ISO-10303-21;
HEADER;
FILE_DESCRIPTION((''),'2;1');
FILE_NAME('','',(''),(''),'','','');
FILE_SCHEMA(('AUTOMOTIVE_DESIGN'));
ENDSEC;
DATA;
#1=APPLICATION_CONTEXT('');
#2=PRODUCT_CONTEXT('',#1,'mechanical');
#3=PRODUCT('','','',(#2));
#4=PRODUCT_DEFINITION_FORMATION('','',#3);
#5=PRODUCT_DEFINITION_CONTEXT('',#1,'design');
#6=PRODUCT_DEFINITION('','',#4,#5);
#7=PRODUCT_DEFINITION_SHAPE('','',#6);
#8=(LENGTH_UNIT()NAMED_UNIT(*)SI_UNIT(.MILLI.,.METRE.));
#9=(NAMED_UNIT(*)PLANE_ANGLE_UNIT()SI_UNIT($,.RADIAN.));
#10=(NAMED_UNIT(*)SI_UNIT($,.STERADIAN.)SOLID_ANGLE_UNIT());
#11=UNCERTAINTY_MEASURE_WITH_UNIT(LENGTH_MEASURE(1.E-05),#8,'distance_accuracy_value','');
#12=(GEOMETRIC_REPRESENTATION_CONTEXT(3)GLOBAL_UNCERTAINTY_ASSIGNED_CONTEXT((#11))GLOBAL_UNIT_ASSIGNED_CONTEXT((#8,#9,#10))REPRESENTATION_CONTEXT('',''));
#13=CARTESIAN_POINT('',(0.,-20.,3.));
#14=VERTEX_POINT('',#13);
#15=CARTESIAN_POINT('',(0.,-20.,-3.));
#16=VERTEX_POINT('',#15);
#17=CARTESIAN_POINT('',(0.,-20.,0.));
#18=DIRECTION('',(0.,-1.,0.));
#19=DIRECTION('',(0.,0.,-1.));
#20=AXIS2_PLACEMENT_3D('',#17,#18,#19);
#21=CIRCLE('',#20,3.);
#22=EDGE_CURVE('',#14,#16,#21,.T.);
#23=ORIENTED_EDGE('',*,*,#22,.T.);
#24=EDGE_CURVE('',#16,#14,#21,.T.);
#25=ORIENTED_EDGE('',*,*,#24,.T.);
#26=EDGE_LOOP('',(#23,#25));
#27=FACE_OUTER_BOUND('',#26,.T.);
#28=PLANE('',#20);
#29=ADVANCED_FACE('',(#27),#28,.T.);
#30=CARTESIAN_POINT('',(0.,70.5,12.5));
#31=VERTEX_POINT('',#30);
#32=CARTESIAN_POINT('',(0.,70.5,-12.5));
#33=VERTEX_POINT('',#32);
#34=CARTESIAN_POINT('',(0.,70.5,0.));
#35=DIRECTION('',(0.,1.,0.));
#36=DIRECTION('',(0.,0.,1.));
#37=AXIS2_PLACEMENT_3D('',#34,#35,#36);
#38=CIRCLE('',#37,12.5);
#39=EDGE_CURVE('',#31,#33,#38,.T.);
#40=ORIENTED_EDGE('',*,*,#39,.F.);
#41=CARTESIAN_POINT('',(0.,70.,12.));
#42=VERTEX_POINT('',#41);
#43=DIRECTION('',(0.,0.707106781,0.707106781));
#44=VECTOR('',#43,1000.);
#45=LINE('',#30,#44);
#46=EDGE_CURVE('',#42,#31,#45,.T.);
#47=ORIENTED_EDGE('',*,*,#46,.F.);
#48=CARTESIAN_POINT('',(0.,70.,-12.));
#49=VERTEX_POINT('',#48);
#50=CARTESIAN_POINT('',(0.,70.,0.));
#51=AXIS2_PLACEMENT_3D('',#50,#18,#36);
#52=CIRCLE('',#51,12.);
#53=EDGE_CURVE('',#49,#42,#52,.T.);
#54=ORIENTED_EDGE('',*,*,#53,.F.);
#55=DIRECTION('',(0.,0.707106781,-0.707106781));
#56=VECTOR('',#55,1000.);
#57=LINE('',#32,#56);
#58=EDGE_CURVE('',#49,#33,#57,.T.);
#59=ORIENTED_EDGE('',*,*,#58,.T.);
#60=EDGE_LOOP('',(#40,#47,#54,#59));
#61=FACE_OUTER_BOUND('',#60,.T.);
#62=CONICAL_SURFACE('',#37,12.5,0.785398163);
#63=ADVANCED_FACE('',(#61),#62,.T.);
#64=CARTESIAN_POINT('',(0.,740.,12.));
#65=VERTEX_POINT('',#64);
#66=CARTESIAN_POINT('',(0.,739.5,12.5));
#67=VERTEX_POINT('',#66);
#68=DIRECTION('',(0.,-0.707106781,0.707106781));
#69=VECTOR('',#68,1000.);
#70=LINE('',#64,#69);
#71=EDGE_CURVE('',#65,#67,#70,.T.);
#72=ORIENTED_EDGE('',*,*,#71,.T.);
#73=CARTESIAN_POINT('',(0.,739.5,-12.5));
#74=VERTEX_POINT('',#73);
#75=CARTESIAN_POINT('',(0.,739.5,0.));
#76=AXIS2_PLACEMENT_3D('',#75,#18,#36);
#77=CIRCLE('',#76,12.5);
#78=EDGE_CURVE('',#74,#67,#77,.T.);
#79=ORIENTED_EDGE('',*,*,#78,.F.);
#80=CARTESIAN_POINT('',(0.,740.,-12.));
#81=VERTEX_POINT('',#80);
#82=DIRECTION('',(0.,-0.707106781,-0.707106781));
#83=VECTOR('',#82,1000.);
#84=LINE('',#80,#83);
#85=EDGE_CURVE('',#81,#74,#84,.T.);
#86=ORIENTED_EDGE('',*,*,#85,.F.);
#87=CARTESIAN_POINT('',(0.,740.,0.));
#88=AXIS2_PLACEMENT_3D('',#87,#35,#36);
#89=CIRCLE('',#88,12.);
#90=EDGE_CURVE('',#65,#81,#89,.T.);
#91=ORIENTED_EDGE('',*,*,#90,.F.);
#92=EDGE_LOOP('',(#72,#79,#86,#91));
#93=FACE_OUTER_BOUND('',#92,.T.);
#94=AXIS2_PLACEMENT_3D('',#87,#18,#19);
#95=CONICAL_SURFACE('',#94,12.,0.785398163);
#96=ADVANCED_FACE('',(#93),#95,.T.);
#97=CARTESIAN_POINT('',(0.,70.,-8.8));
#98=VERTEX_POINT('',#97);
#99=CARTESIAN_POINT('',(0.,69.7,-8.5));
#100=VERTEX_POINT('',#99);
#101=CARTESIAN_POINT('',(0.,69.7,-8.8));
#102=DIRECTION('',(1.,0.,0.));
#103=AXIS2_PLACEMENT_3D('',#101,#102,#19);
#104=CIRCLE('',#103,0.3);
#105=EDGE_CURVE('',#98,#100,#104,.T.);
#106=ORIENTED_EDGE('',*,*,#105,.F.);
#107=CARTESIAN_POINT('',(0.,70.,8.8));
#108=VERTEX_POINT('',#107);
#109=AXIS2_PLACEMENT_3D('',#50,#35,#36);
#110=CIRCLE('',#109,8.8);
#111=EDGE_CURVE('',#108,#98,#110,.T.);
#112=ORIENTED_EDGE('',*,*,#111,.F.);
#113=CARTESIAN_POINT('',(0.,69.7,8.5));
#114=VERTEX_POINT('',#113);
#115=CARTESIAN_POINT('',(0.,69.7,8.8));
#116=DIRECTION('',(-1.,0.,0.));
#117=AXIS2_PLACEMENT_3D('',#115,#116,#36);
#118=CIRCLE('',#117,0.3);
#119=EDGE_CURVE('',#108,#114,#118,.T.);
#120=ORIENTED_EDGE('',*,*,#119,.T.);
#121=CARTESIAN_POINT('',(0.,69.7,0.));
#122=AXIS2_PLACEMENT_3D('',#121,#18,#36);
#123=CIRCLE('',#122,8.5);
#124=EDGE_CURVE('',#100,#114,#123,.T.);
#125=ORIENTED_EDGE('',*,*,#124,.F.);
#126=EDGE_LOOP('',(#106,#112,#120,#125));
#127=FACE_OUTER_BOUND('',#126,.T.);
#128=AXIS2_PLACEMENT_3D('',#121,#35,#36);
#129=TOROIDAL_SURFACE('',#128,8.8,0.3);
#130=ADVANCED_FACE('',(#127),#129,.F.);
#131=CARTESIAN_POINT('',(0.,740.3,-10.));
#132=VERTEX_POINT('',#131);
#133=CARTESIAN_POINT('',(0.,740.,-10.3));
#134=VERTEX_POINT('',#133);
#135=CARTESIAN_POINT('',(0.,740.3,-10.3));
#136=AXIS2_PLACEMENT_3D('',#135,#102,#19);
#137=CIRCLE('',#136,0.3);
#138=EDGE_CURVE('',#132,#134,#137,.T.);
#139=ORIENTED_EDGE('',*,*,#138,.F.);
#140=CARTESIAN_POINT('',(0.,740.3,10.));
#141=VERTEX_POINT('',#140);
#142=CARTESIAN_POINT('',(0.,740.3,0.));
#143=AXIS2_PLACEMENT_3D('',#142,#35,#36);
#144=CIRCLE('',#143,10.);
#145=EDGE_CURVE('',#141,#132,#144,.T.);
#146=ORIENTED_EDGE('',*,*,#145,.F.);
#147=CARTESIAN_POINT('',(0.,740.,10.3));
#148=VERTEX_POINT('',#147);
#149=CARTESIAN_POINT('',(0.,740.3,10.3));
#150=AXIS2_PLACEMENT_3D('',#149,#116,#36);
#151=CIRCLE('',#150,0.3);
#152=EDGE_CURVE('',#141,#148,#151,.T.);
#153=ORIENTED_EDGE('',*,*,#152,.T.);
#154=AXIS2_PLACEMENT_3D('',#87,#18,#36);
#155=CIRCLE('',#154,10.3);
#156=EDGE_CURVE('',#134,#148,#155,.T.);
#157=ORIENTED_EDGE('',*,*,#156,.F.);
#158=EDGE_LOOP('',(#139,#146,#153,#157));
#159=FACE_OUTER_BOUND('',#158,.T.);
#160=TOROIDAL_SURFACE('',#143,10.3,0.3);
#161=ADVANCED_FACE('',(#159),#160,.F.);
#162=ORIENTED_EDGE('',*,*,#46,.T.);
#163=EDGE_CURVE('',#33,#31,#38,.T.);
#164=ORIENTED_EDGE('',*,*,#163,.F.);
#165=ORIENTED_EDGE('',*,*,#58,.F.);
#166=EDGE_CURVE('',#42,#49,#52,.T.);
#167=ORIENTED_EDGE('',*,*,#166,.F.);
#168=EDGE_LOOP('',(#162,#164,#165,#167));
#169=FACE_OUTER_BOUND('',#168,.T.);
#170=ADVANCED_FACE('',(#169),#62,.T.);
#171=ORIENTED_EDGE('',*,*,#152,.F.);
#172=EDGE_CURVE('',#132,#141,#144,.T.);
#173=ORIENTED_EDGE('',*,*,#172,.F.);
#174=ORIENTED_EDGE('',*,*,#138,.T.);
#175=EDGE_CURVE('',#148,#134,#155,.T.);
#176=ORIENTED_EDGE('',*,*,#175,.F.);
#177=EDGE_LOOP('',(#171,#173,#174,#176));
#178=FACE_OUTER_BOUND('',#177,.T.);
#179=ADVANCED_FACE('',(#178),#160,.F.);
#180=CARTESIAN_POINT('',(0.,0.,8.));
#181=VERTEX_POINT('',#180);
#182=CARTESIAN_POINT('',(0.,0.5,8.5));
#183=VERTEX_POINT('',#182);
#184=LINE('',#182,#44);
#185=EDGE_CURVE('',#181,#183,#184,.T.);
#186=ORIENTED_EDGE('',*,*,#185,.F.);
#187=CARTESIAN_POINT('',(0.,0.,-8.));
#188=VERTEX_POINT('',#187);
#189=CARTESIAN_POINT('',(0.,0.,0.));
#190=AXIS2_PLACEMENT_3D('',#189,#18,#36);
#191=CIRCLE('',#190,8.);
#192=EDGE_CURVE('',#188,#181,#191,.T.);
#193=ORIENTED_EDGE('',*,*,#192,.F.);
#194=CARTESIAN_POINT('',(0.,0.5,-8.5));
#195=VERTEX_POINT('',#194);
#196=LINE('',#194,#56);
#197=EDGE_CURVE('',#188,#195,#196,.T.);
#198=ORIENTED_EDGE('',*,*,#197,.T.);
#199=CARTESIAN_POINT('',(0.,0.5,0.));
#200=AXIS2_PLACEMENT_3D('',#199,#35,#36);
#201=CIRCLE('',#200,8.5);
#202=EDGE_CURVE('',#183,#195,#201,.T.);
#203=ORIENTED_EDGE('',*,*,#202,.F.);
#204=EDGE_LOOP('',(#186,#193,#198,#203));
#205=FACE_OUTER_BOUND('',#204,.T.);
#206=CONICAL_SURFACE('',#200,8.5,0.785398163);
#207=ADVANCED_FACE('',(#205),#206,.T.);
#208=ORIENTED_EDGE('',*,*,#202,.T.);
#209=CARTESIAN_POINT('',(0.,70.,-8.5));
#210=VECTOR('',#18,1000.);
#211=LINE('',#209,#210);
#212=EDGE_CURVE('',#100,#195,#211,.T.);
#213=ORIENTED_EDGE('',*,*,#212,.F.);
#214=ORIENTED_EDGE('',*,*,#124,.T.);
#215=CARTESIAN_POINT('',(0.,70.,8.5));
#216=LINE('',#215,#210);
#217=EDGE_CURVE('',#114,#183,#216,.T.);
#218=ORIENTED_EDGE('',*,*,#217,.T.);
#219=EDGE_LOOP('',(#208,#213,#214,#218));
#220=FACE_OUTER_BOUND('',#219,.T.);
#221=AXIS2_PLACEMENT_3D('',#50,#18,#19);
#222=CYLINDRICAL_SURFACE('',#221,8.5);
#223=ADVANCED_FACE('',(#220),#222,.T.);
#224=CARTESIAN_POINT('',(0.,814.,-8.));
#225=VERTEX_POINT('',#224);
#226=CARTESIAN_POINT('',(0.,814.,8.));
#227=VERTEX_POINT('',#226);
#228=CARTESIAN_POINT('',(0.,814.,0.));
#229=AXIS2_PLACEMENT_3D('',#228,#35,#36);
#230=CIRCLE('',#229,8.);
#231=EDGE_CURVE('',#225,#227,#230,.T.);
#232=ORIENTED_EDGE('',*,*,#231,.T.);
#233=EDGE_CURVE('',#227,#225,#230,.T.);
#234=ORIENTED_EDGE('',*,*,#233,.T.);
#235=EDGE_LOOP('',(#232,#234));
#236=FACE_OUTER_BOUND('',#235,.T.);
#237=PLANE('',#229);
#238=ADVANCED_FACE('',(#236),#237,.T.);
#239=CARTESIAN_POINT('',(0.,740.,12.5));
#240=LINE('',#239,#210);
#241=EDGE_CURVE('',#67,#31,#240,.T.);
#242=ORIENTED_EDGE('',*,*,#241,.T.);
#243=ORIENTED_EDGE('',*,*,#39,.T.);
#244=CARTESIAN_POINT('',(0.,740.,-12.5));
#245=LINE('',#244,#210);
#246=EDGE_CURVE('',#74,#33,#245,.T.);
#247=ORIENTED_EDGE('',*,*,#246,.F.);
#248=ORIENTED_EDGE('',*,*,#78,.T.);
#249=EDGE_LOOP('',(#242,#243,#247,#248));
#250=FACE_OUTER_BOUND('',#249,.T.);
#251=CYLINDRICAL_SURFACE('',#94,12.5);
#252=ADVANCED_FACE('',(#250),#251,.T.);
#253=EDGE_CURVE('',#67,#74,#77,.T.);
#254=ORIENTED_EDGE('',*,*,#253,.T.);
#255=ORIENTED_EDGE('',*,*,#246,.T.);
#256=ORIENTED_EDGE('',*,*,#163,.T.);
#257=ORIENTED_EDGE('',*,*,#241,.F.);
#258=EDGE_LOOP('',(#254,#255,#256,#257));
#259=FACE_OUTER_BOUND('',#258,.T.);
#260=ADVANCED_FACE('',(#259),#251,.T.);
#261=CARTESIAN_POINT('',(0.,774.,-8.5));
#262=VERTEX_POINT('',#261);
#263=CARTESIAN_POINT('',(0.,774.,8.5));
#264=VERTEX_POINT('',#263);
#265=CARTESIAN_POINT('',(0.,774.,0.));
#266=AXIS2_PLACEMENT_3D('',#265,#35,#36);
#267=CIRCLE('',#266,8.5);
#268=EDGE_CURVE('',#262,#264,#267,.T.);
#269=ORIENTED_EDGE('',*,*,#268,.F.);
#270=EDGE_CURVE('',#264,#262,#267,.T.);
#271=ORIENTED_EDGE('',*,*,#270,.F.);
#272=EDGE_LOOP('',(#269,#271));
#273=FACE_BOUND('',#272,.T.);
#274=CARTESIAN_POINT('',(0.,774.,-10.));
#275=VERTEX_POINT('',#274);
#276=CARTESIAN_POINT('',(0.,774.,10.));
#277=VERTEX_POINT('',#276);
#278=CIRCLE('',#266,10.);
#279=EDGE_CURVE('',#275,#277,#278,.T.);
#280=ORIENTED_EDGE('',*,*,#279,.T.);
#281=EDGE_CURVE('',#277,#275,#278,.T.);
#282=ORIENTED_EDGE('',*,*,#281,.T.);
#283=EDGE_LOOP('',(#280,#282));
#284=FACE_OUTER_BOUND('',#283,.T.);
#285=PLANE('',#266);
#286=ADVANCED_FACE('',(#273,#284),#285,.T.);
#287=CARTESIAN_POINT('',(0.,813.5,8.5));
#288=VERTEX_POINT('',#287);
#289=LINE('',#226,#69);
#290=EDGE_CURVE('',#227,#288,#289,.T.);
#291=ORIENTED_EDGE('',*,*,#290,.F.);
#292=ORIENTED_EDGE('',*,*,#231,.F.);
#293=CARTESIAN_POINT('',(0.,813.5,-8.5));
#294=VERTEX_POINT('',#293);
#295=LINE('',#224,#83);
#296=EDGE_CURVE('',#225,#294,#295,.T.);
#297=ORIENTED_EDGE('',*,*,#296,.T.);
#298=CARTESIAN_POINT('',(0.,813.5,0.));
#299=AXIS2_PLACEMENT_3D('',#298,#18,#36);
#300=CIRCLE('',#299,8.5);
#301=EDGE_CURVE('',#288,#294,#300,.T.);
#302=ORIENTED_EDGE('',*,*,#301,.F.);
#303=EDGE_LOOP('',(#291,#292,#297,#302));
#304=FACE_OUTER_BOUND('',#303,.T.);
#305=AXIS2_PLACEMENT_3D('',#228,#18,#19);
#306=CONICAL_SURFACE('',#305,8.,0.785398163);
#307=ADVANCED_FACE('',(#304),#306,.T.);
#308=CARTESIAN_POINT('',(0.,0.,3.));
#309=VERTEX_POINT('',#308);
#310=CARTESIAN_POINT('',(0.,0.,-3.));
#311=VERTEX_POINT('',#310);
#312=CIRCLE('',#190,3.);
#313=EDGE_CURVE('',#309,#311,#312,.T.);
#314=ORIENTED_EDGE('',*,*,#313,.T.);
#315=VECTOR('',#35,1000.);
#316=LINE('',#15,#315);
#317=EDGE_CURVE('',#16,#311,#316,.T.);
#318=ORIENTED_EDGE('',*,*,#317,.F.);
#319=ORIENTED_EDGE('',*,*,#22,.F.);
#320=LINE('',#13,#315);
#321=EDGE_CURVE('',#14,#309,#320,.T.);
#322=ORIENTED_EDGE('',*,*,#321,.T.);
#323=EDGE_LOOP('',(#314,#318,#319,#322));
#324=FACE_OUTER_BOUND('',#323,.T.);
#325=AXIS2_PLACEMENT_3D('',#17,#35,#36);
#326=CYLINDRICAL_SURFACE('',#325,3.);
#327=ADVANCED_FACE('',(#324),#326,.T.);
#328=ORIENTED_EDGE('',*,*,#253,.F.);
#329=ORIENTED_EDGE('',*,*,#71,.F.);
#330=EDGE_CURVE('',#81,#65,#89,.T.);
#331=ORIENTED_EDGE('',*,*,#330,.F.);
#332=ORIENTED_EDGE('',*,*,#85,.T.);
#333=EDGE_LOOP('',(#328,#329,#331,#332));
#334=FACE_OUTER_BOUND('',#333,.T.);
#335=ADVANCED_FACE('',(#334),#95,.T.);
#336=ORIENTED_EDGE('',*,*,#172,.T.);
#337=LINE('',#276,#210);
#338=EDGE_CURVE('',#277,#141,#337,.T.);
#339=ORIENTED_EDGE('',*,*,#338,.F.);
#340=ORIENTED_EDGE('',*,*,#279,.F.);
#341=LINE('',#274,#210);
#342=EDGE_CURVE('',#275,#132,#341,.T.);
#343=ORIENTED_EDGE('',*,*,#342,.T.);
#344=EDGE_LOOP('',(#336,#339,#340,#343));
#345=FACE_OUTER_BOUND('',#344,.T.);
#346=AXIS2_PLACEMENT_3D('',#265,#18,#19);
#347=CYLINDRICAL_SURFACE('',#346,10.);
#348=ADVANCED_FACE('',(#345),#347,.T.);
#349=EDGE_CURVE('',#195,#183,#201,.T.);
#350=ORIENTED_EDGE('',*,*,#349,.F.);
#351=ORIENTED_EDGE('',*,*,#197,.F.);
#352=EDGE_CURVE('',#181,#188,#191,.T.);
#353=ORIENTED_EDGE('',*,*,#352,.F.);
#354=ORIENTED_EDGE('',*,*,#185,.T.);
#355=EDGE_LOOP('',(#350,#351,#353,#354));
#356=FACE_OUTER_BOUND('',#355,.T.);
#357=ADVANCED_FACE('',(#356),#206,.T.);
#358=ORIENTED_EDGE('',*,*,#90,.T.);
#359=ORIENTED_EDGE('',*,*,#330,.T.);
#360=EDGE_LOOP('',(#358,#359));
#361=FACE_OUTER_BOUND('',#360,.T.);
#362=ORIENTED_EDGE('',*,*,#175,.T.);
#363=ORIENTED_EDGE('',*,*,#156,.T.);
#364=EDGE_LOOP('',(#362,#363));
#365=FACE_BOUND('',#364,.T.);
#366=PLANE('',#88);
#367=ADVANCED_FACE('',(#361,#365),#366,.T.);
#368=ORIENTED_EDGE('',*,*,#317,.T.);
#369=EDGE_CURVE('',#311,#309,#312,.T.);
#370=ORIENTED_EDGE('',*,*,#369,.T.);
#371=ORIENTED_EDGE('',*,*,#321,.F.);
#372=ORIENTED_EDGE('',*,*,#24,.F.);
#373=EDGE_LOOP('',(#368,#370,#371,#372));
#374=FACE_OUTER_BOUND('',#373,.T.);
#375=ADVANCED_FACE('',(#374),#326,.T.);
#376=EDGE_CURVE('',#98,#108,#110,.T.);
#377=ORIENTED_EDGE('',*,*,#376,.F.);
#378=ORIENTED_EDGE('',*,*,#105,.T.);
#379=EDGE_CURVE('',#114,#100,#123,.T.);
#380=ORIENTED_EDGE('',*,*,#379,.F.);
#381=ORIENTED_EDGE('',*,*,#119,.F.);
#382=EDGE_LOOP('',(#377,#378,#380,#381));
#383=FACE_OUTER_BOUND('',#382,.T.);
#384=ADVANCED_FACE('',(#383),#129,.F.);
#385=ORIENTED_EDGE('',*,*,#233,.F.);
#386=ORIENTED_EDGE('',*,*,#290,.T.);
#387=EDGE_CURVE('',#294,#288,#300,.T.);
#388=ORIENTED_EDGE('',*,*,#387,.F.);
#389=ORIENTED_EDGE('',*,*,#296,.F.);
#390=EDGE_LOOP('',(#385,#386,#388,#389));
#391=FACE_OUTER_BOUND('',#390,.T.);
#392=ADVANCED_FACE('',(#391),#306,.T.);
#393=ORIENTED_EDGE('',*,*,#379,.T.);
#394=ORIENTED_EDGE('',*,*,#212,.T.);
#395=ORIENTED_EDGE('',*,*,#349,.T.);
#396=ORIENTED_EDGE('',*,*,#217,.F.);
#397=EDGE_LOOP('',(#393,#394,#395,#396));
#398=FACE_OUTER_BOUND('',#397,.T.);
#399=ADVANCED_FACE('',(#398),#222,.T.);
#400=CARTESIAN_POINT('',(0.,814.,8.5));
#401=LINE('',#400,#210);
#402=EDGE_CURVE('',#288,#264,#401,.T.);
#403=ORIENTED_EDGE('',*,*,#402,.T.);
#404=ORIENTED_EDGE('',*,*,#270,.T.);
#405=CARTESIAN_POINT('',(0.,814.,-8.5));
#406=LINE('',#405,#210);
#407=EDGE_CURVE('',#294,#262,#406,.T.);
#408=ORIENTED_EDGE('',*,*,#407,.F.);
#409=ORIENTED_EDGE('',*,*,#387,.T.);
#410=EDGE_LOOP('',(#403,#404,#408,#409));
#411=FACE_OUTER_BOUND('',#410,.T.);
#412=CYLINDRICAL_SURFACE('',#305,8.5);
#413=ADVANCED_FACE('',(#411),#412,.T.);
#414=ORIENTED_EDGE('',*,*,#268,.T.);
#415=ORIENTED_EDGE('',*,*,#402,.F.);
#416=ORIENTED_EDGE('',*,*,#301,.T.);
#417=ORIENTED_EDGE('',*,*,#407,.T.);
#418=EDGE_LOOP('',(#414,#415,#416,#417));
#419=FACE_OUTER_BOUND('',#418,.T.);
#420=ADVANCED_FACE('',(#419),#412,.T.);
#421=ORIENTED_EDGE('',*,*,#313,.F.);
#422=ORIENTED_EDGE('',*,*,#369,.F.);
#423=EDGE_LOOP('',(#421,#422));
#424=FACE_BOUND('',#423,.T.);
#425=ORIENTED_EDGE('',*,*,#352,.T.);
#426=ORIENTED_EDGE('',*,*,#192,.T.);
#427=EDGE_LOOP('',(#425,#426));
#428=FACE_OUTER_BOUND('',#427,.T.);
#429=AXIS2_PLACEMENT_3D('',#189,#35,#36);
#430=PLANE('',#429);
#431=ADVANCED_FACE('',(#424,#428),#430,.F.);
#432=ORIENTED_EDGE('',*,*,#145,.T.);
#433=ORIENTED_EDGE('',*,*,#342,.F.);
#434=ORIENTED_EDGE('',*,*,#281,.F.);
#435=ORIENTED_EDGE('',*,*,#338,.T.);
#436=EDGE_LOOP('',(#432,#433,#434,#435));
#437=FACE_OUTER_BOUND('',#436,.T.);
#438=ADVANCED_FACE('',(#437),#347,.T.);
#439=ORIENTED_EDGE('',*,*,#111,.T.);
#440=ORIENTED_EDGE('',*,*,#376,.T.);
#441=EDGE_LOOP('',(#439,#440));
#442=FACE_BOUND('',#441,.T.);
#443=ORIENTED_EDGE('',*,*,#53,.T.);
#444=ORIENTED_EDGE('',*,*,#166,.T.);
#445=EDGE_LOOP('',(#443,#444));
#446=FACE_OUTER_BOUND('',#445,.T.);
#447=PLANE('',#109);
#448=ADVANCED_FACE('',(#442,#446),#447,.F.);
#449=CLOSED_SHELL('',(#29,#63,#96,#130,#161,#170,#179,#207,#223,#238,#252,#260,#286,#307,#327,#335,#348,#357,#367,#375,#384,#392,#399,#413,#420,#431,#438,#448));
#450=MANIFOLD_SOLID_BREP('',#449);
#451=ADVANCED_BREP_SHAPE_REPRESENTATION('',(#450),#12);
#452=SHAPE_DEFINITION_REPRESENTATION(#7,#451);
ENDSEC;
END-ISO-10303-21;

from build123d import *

# Parameters (mm, degrees)
SKETCH_1_R      = 8.5
EXTRUDE_1_DEPTH = 70
SKETCH_2_R      = 12.5
EXTRUDE_2_DEPTH = 670
SKETCH_3_R      = 10
EXTRUDE_3_DEPTH = 34
SKETCH_4_R      = 8.5
EXTRUDE_4_DEPTH = 40
CHAMFER_1_SIZE  = 0.5
FILLET_1_R      = 0.3
FILLET_2_R      = 0.3
SKETCH_5_R      = 3
EXTRUDE_5_DEPTH = 20


with BuildPart() as part:
    # 草图1 → 拉伸1 (new body)
    with BuildSketch(Plane(origin=(0, 0, 0), x_dir=(1, 0, 0), z_dir=(0, 1, 0))):
        with Locations(Location((0, 0, 0), (0, 0, 270))):
            Circle(SKETCH_1_R)
    extrude(amount=EXTRUDE_1_DEPTH)

    # 草图2 → 拉伸2 (add)
    with BuildSketch(Plane(origin=(0, 70, 0), x_dir=(-1, 0, 0), z_dir=(0, 1, 0))):
        with Locations(Location((0, 0, 0), (0, 0, 90))):
            Circle(SKETCH_2_R)
    extrude(amount=EXTRUDE_2_DEPTH)

    # 草图3 → 拉伸3 (add)
    with BuildSketch(Plane(origin=(0, 740, 0), x_dir=(-1, 0, 0), z_dir=(0, 1, 0))):
        with Locations(Location((0, 0, 0), (0, 0, 90))):
            Circle(SKETCH_3_R)
    extrude(amount=EXTRUDE_3_DEPTH)

    # 草图4 → 拉伸4 (add)
    with BuildSketch(Plane(origin=(0, 774, 0), x_dir=(-1, 0, 0), z_dir=(0, 1, 0))):
        with Locations(Location((0, 0, 0), (0, 0, 90))):
            Circle(SKETCH_4_R)
    extrude(amount=EXTRUDE_4_DEPTH)

    # 倒角1
    chamfer_1_edges = [part.edges().sort_by_distance(p)[0] for p in [
        (0, 814, -8.5),
        (0, 0, -8.5),
        (0, 70, -12.5),
        (0, 740, -12.5),
    ]]
    chamfer(chamfer_1_edges, length=CHAMFER_1_SIZE)

    # 圆角1
    fillet_1_edges = [part.edges().sort_by_distance(p)[0] for p in [
        (0, 70, -8.5),
    ]]
    fillet(fillet_1_edges, radius=FILLET_1_R)

    # 圆角2
    fillet_2_edges = [part.edges().sort_by_distance(p)[0] for p in [
        (0, 740, -10),
    ]]
    fillet(fillet_2_edges, radius=FILLET_2_R)

    # 草图5 → 拉伸5 (add)
    with BuildSketch(Plane.XZ):
        with Locations(Location((0, 0, 0), (0, 0, 90))):
            Circle(SKETCH_5_R)
    extrude(amount=EXTRUDE_5_DEPTH)


solid = part.part
